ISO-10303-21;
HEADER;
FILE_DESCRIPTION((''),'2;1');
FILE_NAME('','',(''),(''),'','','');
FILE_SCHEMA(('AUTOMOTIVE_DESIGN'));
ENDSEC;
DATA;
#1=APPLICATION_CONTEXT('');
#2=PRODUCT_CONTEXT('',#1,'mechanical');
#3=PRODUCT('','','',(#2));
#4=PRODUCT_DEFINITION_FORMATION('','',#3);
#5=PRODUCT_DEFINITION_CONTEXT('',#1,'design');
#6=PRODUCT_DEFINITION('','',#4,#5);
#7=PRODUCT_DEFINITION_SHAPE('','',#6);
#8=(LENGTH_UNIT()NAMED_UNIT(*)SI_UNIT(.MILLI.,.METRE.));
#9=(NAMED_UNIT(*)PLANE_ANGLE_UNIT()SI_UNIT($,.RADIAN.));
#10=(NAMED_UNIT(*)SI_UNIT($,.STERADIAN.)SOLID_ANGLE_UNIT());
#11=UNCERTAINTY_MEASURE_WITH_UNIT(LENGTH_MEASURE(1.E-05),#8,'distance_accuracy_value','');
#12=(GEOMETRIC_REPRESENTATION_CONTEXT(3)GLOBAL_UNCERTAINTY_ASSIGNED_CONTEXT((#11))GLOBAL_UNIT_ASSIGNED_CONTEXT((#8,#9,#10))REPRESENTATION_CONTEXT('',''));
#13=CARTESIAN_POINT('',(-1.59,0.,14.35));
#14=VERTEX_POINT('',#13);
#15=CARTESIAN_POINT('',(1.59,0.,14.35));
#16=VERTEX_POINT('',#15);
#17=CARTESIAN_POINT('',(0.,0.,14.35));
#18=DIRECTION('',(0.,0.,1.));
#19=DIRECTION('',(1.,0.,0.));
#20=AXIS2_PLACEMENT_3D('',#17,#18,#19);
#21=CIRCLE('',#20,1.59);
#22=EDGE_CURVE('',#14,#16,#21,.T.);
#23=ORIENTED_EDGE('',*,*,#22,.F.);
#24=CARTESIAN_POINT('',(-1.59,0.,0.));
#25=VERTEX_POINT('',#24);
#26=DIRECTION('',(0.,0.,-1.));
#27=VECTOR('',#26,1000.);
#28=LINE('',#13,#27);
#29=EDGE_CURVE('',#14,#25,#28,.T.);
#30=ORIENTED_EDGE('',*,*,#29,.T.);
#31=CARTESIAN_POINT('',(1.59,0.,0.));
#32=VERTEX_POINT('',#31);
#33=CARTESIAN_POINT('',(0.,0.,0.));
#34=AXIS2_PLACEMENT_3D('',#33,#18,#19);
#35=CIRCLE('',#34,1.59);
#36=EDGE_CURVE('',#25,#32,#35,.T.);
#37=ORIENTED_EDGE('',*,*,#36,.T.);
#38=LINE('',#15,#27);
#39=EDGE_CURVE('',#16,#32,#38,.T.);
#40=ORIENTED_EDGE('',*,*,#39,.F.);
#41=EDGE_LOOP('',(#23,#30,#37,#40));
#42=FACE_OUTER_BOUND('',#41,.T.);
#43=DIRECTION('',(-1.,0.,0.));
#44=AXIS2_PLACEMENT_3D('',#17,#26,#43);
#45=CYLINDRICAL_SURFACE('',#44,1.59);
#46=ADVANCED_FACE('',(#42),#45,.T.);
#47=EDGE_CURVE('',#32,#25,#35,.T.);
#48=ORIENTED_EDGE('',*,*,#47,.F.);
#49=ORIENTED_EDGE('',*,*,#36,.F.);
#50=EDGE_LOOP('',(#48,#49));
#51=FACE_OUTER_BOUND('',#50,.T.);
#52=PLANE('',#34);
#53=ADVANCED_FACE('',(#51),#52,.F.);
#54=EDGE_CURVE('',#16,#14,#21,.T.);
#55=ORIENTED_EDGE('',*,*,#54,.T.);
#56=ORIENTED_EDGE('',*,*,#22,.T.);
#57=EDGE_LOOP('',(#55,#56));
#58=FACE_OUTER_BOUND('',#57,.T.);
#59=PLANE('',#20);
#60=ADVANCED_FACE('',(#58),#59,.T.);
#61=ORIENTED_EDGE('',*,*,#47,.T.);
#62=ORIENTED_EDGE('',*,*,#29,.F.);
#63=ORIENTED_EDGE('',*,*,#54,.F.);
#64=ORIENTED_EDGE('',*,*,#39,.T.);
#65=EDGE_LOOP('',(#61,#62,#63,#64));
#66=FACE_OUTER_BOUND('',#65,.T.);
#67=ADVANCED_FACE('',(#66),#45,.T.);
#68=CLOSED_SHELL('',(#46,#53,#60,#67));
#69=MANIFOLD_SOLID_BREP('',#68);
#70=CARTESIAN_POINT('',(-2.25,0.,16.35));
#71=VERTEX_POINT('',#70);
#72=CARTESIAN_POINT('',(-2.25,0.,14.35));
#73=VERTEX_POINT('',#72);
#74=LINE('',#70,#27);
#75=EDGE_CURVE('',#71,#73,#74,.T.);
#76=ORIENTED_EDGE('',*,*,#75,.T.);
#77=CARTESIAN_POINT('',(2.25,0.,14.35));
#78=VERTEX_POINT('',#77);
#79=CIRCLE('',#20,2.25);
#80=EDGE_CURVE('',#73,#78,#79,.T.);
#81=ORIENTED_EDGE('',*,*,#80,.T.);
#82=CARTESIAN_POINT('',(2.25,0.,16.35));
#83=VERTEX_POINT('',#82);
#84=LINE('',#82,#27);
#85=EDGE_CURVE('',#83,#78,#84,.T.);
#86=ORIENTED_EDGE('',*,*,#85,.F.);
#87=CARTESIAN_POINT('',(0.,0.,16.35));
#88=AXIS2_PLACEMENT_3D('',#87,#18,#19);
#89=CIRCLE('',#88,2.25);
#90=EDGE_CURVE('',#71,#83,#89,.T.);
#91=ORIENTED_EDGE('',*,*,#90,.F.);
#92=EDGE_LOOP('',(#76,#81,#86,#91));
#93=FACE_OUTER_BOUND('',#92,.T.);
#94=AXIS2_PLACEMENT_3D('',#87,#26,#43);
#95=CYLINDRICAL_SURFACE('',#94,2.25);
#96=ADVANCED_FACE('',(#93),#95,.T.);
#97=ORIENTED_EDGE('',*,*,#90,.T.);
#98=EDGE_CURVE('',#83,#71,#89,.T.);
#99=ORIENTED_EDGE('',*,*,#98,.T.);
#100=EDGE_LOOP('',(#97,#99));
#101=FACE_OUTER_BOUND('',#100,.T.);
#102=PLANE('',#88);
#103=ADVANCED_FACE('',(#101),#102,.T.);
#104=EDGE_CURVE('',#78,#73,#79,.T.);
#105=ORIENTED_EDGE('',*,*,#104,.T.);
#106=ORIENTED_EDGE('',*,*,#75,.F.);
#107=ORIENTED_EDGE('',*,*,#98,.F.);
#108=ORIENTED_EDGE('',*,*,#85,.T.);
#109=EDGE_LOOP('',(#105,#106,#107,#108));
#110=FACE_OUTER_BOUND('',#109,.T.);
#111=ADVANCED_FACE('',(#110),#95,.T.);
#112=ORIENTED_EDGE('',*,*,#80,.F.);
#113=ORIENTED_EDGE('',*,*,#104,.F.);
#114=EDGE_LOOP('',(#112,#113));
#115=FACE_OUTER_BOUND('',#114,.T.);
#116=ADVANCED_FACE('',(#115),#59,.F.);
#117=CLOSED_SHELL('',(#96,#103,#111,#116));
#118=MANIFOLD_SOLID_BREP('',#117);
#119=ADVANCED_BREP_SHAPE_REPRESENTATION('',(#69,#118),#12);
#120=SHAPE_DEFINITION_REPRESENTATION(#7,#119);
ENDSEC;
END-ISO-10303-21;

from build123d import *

# Parameters (mm, degrees)
SKETCH_1_R      = 1.59
EXTRUDE_1_DEPTH = 14.35
SKETCH_2_R      = 2.25
EXTRUDE_2_DEPTH = 2


with BuildPart() as part:
    # 草图1 → 凸台-拉伸1 (new body)
    with BuildSketch(Plane.XY):
        Circle(SKETCH_1_R)
    extrude(amount=EXTRUDE_1_DEPTH)


with BuildPart() as body_2:
    # 草图2 → 凸台-拉伸2 (new body)
    with BuildSketch(Plane.XY.offset(14.35)):
        Circle(SKETCH_2_R)
    extrude(amount=EXTRUDE_2_DEPTH)


solid = Compound([part.part, body_2.part])
